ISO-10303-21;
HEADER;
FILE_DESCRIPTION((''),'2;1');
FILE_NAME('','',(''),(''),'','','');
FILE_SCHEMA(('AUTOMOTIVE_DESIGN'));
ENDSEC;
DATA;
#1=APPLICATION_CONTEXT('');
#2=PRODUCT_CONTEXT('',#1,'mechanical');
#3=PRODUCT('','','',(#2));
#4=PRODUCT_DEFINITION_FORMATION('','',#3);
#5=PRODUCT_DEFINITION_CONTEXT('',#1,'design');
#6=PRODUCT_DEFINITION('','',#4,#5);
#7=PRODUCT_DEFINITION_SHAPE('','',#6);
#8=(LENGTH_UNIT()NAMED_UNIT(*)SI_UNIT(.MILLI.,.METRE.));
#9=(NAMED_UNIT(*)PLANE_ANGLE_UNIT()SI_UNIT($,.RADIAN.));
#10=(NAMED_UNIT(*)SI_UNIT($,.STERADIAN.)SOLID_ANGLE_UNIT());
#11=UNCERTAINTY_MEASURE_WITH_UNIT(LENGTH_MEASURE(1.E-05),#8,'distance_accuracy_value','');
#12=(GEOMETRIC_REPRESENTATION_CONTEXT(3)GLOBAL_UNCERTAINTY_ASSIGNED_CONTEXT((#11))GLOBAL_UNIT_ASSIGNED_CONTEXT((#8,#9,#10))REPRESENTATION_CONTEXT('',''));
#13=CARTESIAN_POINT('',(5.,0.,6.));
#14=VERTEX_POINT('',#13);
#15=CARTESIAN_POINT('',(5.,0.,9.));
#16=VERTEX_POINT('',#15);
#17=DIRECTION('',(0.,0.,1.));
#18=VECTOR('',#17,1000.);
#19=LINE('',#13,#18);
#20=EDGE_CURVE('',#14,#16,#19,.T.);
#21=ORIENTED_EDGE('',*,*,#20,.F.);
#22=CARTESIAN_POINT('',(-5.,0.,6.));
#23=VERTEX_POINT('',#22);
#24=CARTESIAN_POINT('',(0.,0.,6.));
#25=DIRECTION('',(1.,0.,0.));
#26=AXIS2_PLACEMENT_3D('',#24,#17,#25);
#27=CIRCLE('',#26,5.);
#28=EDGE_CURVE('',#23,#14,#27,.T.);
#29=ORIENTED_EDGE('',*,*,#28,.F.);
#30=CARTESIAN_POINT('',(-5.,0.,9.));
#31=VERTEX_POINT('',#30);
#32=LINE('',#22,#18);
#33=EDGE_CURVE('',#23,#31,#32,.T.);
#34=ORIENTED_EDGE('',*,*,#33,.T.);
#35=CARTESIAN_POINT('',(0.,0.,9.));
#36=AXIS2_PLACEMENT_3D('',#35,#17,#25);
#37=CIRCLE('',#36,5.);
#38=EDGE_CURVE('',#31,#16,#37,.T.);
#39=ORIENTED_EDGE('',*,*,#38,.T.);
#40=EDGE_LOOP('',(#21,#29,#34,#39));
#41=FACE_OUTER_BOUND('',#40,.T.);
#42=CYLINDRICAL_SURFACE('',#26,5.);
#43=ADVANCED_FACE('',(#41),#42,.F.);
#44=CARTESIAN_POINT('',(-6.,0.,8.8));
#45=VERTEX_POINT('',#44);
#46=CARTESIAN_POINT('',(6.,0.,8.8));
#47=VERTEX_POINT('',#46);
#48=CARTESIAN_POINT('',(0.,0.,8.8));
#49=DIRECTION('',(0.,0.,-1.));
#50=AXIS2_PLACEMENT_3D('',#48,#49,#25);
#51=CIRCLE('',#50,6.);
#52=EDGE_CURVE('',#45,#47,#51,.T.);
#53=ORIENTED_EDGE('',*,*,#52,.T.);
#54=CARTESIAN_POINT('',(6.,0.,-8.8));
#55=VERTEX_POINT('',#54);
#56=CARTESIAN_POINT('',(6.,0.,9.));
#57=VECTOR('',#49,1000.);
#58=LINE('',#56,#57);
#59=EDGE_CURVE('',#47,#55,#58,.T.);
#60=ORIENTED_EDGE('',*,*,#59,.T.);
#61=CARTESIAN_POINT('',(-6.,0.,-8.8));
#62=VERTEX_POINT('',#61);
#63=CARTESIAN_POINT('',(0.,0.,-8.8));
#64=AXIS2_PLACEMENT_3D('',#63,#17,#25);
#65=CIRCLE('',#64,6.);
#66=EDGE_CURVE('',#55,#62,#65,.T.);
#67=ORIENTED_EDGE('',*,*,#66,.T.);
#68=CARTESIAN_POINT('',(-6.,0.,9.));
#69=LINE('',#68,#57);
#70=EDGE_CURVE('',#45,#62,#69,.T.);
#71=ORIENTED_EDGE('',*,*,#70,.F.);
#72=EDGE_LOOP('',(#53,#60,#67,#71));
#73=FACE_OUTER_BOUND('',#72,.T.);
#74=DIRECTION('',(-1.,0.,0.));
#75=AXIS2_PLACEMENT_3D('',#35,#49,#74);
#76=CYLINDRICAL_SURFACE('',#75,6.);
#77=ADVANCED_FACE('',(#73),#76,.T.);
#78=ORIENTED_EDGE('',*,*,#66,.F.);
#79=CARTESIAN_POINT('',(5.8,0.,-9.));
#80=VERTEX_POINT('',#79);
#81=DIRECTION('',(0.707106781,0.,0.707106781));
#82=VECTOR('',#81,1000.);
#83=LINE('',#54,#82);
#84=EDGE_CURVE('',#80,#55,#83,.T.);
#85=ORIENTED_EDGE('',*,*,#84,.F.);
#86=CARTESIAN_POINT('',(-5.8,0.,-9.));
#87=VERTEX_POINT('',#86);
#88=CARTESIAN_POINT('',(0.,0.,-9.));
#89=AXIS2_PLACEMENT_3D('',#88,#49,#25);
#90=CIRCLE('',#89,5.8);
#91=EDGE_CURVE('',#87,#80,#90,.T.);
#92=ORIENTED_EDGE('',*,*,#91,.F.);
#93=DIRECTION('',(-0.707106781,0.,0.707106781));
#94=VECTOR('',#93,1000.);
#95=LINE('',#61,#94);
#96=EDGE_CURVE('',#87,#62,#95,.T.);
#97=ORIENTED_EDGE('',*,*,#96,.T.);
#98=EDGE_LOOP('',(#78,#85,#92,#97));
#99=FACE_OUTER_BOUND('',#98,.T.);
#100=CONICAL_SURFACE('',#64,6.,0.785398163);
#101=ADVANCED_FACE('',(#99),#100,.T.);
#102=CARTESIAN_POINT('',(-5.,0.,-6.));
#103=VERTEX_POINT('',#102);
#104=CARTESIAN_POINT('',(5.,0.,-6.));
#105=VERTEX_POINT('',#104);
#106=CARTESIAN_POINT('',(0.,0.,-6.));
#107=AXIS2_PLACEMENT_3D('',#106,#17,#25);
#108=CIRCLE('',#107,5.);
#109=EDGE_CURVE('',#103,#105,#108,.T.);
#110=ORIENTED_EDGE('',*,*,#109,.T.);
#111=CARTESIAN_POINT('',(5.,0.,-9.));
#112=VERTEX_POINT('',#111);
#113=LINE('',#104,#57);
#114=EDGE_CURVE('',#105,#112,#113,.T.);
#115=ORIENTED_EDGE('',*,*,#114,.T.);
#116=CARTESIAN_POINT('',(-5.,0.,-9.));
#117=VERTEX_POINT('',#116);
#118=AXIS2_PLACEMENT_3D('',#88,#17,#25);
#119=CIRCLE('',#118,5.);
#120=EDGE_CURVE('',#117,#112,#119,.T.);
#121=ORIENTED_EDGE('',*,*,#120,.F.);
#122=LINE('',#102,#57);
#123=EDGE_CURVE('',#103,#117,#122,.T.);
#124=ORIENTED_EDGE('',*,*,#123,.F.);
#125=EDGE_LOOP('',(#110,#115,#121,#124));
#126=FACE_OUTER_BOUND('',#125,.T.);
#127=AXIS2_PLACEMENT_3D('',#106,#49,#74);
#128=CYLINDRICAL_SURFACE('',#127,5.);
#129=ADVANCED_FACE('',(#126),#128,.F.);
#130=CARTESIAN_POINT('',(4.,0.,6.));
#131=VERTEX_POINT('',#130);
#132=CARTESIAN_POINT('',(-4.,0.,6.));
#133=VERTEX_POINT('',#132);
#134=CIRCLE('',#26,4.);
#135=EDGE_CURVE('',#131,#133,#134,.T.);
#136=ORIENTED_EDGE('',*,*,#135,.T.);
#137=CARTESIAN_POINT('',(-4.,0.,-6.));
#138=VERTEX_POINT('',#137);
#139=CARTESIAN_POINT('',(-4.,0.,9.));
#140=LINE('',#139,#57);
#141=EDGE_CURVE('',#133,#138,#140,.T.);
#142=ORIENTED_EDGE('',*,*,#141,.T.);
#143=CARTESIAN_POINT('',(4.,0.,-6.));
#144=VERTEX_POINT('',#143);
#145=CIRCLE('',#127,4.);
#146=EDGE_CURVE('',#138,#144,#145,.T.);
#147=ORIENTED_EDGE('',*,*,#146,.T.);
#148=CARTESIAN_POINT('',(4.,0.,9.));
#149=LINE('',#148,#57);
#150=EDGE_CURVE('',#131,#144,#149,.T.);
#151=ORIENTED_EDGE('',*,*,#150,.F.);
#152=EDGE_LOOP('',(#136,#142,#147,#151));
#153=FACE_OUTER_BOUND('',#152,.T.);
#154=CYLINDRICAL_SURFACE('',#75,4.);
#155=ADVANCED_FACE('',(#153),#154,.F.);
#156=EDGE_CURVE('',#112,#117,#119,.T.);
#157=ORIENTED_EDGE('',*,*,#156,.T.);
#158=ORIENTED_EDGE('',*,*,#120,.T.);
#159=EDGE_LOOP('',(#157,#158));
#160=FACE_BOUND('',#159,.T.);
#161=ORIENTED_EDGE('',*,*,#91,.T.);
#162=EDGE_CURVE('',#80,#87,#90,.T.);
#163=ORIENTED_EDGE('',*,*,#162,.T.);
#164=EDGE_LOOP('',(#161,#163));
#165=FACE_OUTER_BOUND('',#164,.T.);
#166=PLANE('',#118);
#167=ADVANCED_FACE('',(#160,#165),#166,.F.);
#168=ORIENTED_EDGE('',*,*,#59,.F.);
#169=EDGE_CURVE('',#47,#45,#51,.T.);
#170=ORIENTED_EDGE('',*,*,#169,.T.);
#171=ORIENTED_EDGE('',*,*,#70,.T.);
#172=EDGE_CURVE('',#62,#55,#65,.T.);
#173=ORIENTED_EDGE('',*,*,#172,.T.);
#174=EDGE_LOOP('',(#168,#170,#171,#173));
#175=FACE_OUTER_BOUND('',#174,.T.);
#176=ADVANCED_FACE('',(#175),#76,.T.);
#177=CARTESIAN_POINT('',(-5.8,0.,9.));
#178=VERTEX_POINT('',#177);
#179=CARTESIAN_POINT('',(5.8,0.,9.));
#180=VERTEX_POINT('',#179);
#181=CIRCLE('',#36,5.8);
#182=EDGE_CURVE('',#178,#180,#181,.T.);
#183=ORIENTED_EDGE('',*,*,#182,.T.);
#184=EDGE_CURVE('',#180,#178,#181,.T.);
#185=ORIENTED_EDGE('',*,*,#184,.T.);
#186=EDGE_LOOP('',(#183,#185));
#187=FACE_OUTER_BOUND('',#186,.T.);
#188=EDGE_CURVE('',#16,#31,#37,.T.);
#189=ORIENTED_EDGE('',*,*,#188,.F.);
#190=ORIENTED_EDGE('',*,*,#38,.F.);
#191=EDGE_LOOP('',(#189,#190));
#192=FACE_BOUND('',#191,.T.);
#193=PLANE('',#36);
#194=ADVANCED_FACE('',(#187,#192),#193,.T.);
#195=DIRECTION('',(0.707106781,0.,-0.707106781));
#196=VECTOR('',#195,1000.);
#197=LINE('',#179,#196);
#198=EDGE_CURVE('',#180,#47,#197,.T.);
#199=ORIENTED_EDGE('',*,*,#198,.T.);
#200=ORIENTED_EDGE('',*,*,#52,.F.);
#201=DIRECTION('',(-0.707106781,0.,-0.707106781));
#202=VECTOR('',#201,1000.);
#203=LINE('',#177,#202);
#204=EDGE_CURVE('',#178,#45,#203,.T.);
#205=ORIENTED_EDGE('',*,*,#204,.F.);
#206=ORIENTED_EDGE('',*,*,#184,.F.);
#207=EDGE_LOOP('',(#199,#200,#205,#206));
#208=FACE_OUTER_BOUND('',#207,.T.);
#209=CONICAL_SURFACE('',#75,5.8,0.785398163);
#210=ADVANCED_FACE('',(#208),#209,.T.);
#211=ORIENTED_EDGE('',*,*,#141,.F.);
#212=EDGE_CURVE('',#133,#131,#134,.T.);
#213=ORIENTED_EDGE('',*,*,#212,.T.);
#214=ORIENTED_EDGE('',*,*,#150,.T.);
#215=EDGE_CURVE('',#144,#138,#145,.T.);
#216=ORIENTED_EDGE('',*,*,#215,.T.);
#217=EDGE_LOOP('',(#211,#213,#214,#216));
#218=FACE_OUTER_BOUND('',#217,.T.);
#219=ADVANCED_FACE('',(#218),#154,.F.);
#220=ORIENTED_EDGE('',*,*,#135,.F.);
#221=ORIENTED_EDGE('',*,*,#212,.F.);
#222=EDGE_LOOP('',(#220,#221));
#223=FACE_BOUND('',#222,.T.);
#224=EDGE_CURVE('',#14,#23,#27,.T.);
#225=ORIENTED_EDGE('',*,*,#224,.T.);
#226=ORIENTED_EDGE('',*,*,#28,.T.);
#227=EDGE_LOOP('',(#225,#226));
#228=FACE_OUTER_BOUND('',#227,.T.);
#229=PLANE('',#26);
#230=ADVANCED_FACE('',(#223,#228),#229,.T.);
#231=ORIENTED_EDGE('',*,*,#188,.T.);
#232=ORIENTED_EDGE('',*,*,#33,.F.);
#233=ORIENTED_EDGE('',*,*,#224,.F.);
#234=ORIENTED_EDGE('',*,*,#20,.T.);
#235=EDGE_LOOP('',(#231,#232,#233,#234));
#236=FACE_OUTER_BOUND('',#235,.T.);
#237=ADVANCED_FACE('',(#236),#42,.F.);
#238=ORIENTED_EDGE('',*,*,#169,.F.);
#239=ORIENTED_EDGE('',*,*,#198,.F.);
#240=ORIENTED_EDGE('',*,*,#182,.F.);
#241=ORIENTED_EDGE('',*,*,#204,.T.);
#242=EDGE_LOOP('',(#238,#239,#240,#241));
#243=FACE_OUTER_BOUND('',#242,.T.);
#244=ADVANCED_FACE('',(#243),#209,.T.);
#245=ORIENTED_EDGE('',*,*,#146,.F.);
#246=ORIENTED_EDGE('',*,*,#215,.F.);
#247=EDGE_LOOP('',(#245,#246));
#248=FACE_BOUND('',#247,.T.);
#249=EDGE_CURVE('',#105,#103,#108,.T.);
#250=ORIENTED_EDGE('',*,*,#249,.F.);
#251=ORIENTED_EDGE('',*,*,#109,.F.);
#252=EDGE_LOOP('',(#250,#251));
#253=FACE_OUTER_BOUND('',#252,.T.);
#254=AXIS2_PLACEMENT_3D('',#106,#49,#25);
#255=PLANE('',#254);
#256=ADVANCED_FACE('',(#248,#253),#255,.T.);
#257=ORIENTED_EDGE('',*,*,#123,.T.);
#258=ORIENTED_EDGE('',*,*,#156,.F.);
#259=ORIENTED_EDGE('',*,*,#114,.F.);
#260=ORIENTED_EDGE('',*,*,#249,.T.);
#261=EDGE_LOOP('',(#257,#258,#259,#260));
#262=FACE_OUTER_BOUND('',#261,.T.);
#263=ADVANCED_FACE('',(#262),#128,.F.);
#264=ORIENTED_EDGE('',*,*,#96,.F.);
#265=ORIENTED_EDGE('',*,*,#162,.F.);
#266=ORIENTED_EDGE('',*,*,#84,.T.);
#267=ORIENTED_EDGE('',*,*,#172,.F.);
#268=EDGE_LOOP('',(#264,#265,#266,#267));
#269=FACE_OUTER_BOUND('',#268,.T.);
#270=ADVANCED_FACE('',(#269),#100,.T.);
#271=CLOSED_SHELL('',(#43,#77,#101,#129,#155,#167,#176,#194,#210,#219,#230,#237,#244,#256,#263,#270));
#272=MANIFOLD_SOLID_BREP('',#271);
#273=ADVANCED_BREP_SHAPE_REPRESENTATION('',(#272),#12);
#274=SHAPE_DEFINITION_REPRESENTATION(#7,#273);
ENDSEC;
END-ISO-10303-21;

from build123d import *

# Parameters (mm, degrees)
SKETCH1_R           = 6
SKETCH1_R_2         = 4
BOSS_EXTRUDE1_DEPTH = 9
SKETCH2_R           = 5
CUT_EXTRUDE1_DEPTH  = 3
CHAMFER1_SIZE       = 0.2


with BuildPart() as part:
    # Sketch1 → Boss-Extrude1 (new, symmetric)
    with BuildSketch(Plane.XY):
        Circle(SKETCH1_R)
        Circle(SKETCH1_R_2, mode=Mode.SUBTRACT)
    extrude(amount=BOSS_EXTRUDE1_DEPTH, both=True)

    # Sketch2 → Cut-Extrude1 (cut)
    with BuildSketch(Plane.XY.offset(9)):
        Circle(SKETCH2_R)
    cut_extrude1 = extrude(amount=-CUT_EXTRUDE1_DEPTH, mode=Mode.SUBTRACT)

    # Mirror1: Cut-Extrude1 across plane
    add(cut_extrude1.mirror(Plane.XY), mode=Mode.SUBTRACT)

    # Chamfer1
    chamfer1_edges = [part.edges().sort_by_distance(p)[0] for p in [
        (-6, 0, -9),
        (-6, 0, 9),
    ]]
    chamfer(chamfer1_edges, length=CHAMFER1_SIZE)


solid = part.part
